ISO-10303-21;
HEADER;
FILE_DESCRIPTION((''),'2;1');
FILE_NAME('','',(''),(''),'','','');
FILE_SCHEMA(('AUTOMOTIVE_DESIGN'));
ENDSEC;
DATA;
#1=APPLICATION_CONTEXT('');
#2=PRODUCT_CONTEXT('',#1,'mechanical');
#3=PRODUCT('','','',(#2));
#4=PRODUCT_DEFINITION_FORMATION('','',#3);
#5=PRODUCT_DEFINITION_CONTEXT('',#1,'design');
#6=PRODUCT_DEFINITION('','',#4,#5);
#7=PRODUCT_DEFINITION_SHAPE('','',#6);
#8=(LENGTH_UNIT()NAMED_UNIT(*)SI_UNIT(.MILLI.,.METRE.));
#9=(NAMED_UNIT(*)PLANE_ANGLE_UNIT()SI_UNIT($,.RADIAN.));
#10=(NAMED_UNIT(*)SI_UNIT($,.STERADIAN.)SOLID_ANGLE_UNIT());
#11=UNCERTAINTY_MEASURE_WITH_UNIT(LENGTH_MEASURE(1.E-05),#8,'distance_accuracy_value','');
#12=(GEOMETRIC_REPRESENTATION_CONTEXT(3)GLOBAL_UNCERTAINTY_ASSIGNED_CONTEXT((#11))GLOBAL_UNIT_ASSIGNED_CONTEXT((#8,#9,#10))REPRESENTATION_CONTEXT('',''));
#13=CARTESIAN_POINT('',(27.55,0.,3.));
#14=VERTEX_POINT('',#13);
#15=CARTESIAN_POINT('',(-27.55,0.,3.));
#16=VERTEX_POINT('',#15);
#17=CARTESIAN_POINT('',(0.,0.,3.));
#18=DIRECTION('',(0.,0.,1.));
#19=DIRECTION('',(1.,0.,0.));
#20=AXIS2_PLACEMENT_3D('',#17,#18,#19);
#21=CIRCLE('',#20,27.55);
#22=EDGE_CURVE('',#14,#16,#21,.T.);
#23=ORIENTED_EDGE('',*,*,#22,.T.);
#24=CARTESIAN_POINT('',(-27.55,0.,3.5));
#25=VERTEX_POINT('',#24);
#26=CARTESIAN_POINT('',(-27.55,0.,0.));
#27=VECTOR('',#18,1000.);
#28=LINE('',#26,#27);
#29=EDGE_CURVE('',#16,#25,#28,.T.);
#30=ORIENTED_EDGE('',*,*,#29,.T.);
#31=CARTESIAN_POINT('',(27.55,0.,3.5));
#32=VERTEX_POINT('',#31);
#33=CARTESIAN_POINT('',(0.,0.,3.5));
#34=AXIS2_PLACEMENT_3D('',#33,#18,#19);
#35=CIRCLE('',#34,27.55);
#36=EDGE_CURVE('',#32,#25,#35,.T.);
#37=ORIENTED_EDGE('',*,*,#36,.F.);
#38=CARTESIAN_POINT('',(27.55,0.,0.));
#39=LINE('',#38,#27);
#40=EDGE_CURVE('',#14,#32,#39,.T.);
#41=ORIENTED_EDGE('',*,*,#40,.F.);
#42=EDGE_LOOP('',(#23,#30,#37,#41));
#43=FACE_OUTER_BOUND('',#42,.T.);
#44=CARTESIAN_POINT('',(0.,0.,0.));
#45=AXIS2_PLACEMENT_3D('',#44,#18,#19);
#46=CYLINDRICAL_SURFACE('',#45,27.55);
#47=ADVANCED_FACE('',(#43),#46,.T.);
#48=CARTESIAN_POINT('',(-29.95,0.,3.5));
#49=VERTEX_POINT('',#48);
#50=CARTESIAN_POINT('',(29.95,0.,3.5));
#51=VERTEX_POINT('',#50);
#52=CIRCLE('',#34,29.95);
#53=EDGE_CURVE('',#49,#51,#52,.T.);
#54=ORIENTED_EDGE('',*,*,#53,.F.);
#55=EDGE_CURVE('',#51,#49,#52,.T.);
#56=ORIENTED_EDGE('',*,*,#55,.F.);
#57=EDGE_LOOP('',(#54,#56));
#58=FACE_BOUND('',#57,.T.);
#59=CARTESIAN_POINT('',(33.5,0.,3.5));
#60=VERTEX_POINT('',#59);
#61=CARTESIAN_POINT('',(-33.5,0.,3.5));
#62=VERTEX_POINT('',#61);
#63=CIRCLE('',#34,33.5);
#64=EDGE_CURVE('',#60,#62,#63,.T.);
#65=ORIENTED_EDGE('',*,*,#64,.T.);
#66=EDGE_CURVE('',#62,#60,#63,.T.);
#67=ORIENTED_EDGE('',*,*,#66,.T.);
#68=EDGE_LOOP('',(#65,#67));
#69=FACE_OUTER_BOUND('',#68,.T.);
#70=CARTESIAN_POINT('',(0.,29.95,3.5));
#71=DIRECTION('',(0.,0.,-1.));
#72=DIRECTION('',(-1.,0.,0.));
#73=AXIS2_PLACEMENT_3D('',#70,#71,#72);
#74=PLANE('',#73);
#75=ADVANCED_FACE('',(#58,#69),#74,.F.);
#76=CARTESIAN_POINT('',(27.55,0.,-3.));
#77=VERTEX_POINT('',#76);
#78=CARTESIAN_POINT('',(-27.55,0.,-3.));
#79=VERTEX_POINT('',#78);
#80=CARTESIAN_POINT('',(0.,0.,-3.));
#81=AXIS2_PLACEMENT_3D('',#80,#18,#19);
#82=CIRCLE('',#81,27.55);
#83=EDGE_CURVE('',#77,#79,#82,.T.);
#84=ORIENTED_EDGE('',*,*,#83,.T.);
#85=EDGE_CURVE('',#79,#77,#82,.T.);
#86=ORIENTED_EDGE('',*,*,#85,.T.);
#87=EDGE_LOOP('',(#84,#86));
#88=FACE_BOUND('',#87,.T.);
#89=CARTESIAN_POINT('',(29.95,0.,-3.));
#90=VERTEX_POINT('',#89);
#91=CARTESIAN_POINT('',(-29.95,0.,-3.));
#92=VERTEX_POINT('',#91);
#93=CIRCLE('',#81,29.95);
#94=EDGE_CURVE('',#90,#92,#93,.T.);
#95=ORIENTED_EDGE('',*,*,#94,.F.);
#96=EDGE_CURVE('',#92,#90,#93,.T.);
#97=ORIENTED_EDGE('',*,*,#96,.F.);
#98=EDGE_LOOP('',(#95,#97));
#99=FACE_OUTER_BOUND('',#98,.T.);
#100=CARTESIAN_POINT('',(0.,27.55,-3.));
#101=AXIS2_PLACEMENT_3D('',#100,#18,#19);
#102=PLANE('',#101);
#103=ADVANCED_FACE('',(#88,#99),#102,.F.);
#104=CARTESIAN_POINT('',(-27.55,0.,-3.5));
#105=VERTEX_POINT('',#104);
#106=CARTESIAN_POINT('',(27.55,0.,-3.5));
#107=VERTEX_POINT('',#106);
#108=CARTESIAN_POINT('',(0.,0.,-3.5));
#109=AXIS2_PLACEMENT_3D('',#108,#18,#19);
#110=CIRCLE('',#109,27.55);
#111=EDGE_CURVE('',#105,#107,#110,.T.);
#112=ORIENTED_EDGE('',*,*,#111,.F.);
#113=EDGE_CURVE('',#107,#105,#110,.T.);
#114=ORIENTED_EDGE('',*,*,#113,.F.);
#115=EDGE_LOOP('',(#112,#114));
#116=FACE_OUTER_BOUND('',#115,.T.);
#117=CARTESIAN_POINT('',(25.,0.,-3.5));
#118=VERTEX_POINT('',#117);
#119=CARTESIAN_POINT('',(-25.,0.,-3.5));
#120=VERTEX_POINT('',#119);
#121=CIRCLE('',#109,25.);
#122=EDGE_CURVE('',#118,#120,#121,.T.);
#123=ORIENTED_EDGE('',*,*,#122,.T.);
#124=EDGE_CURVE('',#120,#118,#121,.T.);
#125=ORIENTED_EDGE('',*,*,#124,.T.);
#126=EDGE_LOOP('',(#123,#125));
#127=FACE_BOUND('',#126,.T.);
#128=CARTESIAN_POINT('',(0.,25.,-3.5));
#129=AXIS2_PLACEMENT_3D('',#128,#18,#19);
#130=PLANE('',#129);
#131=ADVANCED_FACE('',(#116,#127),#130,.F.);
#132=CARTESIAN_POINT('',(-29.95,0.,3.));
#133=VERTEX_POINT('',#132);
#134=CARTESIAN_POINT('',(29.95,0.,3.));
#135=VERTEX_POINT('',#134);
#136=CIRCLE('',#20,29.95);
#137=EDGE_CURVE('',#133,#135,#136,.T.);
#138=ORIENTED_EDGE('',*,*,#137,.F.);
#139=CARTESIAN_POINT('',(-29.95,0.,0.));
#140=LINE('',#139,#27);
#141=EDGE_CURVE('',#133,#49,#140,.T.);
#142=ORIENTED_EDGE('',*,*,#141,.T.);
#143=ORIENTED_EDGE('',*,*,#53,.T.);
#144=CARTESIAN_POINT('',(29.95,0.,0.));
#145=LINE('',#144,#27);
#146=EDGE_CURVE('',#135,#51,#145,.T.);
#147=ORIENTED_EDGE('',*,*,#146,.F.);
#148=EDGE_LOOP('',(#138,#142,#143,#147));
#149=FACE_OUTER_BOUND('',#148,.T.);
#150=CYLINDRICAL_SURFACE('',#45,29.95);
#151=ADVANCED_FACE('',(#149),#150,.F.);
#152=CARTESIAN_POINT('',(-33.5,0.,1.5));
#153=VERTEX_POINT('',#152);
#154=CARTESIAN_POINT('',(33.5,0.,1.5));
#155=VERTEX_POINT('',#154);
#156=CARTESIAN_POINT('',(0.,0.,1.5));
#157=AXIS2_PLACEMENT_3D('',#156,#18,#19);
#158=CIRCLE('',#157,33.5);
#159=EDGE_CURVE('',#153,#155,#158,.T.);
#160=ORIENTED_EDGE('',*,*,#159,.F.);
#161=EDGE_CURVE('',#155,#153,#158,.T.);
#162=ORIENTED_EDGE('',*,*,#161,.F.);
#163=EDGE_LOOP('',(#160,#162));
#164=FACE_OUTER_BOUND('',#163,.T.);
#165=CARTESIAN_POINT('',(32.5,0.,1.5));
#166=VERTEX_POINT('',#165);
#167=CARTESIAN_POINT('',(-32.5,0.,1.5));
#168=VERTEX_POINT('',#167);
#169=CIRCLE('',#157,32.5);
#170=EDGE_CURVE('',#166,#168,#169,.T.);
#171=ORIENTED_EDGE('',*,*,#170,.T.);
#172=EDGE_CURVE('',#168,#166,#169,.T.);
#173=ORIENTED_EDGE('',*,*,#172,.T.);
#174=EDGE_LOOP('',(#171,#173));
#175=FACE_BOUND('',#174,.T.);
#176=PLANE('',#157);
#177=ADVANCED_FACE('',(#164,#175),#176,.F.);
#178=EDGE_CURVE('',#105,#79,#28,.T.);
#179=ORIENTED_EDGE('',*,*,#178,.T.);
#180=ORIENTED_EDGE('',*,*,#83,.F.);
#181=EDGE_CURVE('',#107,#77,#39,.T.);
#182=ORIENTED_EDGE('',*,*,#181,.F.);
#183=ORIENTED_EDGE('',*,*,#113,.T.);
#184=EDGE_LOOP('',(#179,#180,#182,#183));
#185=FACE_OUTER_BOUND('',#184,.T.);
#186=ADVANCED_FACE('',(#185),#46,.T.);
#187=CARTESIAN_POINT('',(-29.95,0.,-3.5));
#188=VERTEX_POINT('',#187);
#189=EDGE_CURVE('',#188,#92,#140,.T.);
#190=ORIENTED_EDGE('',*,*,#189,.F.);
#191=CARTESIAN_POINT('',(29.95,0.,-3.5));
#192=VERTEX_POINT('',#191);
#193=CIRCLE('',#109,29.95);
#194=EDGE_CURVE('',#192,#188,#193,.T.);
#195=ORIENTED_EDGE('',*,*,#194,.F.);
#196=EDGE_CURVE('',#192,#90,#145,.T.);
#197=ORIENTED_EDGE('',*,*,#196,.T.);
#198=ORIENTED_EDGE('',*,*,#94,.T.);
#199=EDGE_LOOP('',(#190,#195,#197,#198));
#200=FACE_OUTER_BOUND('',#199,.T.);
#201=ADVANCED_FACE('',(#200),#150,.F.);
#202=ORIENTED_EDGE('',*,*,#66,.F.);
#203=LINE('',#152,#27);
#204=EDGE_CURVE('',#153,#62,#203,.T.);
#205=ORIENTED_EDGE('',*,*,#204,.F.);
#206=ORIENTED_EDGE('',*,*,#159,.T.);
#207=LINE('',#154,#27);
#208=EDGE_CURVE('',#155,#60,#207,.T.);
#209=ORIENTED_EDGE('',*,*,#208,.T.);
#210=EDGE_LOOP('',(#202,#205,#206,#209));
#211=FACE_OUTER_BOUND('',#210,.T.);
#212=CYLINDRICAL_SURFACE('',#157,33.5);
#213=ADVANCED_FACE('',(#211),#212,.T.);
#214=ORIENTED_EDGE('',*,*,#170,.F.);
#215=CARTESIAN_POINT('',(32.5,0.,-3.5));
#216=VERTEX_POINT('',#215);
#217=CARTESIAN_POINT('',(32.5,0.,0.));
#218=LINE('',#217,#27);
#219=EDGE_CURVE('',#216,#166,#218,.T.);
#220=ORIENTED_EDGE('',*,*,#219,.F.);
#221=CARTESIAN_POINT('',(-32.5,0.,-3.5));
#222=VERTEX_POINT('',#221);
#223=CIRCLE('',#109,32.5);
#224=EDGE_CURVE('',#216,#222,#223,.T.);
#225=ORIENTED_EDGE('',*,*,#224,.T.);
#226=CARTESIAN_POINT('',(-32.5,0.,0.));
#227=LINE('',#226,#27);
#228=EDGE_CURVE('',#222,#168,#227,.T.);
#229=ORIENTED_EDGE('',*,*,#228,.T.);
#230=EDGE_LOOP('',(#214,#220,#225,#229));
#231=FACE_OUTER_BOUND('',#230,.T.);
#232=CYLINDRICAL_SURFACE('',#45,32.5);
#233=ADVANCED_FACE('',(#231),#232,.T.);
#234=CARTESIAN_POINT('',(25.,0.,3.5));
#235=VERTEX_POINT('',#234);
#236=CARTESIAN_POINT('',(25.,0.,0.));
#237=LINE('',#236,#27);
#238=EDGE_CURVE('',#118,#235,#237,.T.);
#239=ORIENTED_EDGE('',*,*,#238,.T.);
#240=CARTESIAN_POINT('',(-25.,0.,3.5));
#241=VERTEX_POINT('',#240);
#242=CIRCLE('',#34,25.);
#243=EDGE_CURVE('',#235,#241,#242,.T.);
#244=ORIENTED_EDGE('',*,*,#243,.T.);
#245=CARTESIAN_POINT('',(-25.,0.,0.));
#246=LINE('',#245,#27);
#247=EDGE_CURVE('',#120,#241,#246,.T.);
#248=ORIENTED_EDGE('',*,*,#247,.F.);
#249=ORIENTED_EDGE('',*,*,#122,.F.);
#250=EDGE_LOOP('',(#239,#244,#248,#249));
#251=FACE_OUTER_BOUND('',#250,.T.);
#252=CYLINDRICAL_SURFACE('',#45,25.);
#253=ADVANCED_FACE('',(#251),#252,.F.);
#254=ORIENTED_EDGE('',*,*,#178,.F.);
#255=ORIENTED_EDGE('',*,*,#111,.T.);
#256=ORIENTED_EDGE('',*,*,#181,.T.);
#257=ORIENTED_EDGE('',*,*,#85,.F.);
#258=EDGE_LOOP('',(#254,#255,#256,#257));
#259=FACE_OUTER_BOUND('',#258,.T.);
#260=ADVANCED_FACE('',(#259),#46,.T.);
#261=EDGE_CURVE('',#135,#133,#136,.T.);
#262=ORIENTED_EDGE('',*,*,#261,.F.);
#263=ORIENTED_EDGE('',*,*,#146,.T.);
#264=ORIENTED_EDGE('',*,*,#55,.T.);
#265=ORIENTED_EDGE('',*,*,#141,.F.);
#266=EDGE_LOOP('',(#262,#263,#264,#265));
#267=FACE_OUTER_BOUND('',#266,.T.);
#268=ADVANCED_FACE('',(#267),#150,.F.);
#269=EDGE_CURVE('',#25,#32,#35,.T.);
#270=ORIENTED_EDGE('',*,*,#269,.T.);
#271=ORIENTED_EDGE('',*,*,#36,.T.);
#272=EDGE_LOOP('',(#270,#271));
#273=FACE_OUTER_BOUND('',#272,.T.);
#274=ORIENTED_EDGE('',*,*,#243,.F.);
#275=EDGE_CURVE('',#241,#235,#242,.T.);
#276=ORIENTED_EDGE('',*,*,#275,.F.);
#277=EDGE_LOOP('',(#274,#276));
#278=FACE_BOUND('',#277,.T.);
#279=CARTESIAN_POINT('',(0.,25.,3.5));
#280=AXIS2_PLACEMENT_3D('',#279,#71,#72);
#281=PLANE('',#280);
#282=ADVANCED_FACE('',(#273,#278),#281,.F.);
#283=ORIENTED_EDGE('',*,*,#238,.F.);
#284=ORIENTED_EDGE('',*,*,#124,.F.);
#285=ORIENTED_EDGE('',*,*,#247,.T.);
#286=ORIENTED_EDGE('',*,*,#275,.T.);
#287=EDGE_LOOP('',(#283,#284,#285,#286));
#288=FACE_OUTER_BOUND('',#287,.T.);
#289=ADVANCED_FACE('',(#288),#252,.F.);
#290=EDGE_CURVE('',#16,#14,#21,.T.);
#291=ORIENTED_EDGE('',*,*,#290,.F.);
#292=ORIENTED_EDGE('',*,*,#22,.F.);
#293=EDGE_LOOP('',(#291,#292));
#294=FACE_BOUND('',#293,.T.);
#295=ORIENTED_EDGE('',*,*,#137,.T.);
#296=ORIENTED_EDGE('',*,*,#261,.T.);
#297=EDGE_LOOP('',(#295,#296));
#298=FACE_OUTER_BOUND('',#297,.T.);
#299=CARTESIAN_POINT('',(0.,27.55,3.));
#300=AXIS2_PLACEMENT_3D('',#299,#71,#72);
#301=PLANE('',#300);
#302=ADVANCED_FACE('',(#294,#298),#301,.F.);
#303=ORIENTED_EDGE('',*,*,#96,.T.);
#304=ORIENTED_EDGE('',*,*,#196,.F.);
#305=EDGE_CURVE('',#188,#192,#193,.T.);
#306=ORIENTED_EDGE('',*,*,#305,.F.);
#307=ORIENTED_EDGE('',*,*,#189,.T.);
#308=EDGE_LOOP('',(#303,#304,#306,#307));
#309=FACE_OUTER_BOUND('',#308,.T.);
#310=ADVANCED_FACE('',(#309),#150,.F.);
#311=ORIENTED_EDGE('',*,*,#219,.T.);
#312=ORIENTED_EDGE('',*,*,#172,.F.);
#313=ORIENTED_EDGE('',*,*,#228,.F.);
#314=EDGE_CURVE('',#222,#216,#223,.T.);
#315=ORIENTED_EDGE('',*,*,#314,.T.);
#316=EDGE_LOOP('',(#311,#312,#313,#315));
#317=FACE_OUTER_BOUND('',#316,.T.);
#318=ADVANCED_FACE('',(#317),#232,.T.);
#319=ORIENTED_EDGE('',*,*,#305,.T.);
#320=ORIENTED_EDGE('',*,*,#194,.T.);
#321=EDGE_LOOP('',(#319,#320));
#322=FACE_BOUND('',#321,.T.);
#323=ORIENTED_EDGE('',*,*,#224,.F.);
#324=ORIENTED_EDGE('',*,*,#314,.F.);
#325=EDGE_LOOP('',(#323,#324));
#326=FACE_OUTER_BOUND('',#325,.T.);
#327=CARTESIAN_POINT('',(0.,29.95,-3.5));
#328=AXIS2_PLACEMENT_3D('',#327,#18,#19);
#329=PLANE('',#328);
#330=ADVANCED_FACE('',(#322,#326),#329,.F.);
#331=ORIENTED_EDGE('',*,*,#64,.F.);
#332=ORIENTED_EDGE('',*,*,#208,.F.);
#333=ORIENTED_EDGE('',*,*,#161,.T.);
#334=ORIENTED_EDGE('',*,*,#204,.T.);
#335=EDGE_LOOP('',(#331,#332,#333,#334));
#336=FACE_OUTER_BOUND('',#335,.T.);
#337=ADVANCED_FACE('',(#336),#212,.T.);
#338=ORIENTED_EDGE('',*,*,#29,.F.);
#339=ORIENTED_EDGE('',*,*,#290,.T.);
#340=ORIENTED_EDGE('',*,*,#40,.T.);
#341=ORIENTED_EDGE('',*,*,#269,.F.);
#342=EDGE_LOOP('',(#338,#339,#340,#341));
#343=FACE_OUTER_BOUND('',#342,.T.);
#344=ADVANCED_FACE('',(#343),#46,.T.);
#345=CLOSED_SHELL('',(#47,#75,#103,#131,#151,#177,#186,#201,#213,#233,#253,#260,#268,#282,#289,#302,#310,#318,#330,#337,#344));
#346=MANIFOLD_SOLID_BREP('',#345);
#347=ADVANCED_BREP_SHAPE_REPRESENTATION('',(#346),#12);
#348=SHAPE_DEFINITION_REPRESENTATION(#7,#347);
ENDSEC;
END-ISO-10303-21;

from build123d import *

# Parameters (mm, degrees)
EXTRUDE_START   = -2
SKETCH_2_R      = 33.5
SKETCH_2_R_2    = 32.5
EXTRUDE_1_DEPTH = 2


with BuildPart() as part:
    # 草图1 → 旋转1 (revolve)
    with BuildSketch(Plane(origin=(0, 0, 0), x_dir=(0, 0, -1), z_dir=(1, 0, 0)), mode=Mode.PRIVATE) as revolve_1_sk:
        Polygon((-3.5, 25), (-3.5, 27.55), (-3, 27.55), (-3, 29.95), (-3.5, 29.95), (-3.5, 32.5), (3.5, 32.5), (3.5, 29.95), (3, 29.95), (3, 27.55), (3.5, 27.55), (3.5, 25), align=None)
    revolve(revolve_1_sk.sketch.rotate(Axis((0, 0, 0), (0, 0, -1)), 90), axis=Axis((0, 0, 0), (0, 0, -1)))

    # 草图2 → 凸台-拉伸1 (add)
    with BuildSketch(Plane.XY.offset(3.5).offset(EXTRUDE_START)):
        Circle(SKETCH_2_R)
        Circle(SKETCH_2_R_2, mode=Mode.SUBTRACT)
    extrude(amount=EXTRUDE_1_DEPTH)


solid = part.part
